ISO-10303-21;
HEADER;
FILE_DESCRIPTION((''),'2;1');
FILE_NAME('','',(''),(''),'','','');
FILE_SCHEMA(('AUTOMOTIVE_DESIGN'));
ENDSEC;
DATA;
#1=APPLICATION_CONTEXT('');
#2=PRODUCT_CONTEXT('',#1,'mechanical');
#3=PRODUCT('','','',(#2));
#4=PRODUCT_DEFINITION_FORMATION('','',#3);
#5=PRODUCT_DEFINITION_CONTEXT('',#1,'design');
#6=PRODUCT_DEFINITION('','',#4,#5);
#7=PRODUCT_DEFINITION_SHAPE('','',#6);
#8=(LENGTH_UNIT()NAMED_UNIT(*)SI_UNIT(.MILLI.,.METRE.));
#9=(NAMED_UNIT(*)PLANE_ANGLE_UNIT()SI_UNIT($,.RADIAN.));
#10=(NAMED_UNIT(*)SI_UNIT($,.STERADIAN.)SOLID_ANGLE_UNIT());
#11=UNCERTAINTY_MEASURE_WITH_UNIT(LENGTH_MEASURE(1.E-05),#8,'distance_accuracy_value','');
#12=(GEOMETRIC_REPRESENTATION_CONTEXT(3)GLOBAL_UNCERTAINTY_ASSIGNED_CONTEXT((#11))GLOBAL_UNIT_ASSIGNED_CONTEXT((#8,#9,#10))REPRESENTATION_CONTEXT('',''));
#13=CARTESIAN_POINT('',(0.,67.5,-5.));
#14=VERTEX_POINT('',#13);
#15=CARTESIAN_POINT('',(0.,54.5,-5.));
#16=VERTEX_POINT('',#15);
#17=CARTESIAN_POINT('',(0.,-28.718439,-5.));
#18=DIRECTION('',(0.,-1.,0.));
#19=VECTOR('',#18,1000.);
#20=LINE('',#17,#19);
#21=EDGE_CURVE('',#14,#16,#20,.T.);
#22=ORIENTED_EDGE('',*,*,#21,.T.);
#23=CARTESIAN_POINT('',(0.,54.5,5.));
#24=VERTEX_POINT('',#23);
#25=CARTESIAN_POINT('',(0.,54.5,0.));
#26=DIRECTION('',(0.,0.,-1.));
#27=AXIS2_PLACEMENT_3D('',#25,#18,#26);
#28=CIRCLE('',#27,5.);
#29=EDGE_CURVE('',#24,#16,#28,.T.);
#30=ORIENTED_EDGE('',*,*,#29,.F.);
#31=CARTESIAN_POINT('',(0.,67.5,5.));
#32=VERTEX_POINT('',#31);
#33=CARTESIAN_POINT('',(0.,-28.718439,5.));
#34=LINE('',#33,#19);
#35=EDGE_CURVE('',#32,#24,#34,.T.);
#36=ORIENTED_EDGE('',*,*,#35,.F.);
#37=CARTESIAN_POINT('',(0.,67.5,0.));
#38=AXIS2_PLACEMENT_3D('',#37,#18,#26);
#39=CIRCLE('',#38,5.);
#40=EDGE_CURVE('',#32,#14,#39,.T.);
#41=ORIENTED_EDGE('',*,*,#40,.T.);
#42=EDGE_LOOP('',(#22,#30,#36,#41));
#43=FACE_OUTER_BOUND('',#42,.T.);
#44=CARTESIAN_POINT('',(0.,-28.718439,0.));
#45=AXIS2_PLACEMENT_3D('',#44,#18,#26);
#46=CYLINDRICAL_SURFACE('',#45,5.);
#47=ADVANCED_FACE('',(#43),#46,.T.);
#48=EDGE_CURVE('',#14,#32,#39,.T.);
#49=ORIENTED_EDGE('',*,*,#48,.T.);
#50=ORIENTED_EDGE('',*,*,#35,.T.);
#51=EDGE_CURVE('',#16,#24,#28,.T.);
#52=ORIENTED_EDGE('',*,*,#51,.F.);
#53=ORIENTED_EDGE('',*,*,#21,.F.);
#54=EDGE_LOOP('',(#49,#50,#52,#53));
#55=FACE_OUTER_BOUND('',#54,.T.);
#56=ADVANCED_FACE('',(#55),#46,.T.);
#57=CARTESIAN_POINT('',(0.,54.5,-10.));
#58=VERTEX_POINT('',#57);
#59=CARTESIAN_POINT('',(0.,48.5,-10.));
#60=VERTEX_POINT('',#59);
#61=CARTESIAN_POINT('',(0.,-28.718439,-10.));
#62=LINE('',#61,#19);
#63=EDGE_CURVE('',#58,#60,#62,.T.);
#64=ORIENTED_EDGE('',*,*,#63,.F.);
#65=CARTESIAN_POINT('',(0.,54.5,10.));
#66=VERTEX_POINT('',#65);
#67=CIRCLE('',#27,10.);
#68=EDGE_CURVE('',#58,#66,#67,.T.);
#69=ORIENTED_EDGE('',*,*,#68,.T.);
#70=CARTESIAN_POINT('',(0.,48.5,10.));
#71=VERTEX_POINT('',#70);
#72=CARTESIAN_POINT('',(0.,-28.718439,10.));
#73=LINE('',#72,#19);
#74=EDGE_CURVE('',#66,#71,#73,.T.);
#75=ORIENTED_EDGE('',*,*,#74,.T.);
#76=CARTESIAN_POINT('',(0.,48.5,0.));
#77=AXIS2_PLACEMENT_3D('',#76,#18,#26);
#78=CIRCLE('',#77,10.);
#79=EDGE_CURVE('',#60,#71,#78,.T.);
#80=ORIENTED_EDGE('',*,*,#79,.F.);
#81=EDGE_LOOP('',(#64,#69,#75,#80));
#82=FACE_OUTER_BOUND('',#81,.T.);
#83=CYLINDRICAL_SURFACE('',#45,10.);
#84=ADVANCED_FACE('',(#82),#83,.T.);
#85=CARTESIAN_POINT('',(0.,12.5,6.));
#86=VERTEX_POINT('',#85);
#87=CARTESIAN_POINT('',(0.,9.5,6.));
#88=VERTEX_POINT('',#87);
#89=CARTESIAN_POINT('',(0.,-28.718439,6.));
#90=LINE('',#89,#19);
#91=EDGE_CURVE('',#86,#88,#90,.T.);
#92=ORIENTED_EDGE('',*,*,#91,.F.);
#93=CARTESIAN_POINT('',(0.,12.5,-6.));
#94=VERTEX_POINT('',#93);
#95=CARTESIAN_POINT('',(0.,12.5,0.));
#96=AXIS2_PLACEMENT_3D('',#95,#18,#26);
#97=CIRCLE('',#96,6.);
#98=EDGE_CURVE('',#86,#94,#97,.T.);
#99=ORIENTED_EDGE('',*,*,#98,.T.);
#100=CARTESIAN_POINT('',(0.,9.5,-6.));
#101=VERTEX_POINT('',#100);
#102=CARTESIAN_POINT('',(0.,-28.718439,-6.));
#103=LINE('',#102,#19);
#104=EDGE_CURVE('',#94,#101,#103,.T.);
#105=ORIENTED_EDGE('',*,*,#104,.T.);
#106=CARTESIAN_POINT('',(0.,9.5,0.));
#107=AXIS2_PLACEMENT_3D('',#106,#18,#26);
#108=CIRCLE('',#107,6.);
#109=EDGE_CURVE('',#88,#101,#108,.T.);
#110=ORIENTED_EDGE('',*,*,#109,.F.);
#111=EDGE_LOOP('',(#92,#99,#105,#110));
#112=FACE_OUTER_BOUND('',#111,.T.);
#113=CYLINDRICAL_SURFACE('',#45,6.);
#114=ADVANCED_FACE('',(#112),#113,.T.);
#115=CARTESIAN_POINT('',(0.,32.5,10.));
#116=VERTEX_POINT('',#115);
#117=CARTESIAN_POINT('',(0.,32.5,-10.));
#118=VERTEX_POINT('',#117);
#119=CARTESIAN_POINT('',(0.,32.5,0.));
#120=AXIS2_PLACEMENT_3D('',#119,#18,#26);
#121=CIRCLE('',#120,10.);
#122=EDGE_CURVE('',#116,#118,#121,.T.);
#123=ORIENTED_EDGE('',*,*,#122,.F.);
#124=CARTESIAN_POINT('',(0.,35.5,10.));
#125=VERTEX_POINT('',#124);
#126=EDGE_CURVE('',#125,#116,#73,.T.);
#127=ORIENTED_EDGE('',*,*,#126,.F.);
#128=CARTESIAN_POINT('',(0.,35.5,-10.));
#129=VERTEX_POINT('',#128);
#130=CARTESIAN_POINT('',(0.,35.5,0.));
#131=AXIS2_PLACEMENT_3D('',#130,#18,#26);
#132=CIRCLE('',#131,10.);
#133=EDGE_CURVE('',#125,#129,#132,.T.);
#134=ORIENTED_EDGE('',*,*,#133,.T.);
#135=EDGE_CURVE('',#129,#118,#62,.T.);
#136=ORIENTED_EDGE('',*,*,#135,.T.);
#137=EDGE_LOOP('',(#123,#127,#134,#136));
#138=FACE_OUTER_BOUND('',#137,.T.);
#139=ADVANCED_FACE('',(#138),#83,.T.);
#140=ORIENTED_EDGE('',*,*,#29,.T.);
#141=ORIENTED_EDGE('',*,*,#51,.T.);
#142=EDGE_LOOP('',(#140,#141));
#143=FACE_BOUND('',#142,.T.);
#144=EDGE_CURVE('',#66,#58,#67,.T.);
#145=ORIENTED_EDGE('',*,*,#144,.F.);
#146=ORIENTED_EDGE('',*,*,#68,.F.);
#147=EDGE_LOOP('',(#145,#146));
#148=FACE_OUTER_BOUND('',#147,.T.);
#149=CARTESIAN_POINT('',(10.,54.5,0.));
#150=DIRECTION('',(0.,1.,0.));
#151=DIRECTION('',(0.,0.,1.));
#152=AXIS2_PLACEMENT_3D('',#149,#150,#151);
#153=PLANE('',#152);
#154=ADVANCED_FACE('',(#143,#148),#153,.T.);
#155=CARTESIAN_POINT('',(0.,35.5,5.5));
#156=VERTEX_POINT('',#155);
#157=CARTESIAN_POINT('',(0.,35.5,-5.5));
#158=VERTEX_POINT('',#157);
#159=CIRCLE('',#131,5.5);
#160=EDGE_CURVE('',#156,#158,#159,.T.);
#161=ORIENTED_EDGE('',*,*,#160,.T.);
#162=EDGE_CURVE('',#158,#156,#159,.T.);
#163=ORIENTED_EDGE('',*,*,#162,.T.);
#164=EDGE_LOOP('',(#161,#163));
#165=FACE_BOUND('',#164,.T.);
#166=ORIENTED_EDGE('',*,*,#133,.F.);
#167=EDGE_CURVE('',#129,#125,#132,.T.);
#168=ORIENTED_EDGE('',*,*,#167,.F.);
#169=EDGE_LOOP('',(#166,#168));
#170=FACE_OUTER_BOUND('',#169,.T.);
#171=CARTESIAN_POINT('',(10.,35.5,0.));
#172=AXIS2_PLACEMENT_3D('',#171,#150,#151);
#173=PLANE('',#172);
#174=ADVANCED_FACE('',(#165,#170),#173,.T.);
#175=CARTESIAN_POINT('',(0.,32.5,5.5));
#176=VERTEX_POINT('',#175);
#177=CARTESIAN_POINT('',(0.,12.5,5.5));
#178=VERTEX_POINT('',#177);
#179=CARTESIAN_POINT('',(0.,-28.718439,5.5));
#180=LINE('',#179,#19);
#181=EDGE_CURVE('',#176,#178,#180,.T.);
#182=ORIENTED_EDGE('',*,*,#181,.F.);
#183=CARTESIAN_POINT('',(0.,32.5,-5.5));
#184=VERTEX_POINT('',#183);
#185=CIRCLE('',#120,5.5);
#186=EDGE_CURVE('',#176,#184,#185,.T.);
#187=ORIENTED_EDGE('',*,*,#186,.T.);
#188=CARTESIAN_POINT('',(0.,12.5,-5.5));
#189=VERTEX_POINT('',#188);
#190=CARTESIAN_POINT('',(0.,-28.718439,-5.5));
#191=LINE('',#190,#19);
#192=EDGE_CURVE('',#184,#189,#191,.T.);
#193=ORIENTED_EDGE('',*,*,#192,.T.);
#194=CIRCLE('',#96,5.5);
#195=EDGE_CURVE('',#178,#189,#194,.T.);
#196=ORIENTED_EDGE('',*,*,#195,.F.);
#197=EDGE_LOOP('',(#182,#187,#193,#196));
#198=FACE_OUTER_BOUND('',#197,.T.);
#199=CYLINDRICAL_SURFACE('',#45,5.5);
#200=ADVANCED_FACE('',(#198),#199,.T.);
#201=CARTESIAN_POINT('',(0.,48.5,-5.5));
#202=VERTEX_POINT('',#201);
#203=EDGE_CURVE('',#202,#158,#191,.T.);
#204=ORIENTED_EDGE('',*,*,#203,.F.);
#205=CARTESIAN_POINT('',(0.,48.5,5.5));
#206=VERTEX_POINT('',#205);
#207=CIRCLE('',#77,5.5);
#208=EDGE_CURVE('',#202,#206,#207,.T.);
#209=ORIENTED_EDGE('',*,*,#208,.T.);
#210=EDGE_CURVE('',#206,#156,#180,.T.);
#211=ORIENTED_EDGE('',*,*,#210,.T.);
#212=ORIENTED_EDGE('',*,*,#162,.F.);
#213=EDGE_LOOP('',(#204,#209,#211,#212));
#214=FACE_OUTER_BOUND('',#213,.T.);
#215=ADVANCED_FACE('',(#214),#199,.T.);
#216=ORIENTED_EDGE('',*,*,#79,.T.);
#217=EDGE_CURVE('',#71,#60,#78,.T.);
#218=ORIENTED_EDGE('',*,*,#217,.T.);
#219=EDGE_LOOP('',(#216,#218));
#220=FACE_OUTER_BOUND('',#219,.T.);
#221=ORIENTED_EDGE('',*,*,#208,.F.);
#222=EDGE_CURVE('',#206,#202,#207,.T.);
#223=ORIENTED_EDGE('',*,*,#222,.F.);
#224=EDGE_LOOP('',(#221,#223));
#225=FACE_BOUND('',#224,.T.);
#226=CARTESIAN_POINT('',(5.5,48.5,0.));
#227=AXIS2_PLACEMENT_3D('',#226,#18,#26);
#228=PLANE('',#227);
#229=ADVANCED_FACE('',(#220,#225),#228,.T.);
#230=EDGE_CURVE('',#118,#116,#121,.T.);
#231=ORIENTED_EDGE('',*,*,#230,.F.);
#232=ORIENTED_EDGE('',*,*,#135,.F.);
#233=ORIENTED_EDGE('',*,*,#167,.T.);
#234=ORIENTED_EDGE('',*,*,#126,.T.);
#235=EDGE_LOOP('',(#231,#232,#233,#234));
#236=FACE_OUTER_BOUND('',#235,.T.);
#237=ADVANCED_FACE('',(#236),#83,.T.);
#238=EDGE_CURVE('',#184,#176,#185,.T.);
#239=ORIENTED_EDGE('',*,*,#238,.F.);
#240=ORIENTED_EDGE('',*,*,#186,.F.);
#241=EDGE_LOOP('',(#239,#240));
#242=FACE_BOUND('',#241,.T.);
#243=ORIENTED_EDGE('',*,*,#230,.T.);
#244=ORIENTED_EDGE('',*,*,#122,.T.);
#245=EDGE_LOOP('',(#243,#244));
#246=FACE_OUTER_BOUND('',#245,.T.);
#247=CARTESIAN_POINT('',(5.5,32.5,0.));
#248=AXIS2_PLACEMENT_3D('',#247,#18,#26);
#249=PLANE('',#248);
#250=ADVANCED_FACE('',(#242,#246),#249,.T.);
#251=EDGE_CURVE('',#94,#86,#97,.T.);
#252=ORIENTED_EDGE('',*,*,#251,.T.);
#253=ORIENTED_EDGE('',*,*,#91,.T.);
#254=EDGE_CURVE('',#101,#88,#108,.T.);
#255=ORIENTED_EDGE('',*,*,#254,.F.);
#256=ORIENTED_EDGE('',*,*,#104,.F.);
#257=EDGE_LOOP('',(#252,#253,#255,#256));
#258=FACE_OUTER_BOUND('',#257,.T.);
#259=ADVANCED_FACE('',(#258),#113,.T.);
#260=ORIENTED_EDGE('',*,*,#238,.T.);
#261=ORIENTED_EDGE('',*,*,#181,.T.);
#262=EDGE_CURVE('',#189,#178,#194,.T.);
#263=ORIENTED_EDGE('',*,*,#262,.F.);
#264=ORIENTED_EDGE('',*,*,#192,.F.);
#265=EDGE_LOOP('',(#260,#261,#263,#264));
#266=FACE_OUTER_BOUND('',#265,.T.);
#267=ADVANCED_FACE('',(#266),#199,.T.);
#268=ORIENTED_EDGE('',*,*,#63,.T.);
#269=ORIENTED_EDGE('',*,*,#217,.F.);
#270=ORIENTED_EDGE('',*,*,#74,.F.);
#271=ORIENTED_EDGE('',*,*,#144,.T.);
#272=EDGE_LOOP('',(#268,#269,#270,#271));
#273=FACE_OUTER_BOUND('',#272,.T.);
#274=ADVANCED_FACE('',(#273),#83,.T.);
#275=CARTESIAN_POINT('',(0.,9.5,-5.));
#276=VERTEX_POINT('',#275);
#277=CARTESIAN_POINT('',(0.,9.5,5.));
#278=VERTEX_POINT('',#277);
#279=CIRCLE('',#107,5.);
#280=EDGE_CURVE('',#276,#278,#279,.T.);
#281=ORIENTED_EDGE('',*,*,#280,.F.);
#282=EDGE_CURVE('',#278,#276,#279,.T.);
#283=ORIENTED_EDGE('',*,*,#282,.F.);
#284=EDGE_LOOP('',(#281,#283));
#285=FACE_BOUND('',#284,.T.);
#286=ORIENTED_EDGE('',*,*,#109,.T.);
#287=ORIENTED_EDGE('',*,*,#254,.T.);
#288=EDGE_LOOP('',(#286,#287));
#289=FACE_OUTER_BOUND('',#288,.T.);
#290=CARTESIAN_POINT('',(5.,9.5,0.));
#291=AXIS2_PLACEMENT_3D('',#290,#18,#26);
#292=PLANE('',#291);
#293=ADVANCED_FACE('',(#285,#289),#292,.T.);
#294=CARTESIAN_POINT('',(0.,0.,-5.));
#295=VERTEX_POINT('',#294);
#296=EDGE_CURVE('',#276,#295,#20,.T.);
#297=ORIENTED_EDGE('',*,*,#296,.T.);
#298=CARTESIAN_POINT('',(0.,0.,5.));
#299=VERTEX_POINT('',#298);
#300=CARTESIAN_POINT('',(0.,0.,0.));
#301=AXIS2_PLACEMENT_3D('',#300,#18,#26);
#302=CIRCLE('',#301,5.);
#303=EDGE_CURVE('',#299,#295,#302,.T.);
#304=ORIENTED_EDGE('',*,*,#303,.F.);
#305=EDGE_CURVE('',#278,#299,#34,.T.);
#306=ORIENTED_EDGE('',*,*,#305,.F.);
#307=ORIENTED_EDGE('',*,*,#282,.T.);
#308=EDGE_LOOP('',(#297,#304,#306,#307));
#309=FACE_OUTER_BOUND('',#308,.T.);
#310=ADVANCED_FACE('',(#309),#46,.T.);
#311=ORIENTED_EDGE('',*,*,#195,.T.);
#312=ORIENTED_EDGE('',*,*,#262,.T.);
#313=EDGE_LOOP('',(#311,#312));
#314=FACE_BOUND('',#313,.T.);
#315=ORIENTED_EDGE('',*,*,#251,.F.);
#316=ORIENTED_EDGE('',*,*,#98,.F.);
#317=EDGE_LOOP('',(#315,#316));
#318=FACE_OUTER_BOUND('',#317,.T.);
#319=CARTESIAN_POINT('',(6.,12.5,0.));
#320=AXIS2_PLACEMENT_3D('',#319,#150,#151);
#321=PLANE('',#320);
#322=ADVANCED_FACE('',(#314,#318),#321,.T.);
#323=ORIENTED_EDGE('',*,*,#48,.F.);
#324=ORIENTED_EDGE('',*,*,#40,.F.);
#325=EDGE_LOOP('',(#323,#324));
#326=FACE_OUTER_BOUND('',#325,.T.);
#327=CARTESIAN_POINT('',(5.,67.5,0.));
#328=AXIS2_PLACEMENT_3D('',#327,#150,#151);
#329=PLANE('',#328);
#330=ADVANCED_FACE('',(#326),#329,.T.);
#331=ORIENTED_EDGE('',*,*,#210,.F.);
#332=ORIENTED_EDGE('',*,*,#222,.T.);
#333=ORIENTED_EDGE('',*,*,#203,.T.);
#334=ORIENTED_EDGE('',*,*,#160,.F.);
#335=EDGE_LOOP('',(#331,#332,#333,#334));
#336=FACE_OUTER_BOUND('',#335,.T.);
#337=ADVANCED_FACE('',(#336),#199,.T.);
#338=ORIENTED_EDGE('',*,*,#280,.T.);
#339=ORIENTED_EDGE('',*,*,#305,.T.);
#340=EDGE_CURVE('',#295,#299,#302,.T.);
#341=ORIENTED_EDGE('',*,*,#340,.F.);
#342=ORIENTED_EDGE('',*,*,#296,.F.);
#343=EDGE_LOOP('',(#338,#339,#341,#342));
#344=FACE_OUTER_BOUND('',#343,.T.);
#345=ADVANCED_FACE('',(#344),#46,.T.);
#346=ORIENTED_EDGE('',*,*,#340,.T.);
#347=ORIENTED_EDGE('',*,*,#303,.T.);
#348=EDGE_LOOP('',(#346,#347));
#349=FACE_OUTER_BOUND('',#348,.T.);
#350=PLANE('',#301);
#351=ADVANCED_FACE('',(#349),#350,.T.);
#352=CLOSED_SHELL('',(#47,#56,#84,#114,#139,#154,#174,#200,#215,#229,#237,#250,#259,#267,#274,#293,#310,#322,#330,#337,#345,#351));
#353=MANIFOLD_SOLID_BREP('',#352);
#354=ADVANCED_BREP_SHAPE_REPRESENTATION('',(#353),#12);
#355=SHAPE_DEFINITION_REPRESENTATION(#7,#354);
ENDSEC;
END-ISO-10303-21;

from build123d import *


with BuildPart() as part:
    # 草图1 → 旋转1 (revolve)
    with BuildSketch(Plane.XY, mode=Mode.PRIVATE) as revolve_1_sk:
        Polygon((0, 0), (5, 0), (5, 9.5), (6, 9.5), (6, 12.5), (5.5, 12.5), (5.5, 32.5), (10, 32.5), (10, 35.5), (5.5, 35.5), (5.5, 48.5), (10, 48.5), (10, 54.5), (5, 54.5), (5, 67.5), (0, 67.5), align=None)
    revolve(revolve_1_sk.sketch.rotate(Axis((0, -28.718438831, 0), (0, 1, 0)), 90), axis=Axis((0, -28.718438831, 0), (0, 1, 0)))


solid = part.part
